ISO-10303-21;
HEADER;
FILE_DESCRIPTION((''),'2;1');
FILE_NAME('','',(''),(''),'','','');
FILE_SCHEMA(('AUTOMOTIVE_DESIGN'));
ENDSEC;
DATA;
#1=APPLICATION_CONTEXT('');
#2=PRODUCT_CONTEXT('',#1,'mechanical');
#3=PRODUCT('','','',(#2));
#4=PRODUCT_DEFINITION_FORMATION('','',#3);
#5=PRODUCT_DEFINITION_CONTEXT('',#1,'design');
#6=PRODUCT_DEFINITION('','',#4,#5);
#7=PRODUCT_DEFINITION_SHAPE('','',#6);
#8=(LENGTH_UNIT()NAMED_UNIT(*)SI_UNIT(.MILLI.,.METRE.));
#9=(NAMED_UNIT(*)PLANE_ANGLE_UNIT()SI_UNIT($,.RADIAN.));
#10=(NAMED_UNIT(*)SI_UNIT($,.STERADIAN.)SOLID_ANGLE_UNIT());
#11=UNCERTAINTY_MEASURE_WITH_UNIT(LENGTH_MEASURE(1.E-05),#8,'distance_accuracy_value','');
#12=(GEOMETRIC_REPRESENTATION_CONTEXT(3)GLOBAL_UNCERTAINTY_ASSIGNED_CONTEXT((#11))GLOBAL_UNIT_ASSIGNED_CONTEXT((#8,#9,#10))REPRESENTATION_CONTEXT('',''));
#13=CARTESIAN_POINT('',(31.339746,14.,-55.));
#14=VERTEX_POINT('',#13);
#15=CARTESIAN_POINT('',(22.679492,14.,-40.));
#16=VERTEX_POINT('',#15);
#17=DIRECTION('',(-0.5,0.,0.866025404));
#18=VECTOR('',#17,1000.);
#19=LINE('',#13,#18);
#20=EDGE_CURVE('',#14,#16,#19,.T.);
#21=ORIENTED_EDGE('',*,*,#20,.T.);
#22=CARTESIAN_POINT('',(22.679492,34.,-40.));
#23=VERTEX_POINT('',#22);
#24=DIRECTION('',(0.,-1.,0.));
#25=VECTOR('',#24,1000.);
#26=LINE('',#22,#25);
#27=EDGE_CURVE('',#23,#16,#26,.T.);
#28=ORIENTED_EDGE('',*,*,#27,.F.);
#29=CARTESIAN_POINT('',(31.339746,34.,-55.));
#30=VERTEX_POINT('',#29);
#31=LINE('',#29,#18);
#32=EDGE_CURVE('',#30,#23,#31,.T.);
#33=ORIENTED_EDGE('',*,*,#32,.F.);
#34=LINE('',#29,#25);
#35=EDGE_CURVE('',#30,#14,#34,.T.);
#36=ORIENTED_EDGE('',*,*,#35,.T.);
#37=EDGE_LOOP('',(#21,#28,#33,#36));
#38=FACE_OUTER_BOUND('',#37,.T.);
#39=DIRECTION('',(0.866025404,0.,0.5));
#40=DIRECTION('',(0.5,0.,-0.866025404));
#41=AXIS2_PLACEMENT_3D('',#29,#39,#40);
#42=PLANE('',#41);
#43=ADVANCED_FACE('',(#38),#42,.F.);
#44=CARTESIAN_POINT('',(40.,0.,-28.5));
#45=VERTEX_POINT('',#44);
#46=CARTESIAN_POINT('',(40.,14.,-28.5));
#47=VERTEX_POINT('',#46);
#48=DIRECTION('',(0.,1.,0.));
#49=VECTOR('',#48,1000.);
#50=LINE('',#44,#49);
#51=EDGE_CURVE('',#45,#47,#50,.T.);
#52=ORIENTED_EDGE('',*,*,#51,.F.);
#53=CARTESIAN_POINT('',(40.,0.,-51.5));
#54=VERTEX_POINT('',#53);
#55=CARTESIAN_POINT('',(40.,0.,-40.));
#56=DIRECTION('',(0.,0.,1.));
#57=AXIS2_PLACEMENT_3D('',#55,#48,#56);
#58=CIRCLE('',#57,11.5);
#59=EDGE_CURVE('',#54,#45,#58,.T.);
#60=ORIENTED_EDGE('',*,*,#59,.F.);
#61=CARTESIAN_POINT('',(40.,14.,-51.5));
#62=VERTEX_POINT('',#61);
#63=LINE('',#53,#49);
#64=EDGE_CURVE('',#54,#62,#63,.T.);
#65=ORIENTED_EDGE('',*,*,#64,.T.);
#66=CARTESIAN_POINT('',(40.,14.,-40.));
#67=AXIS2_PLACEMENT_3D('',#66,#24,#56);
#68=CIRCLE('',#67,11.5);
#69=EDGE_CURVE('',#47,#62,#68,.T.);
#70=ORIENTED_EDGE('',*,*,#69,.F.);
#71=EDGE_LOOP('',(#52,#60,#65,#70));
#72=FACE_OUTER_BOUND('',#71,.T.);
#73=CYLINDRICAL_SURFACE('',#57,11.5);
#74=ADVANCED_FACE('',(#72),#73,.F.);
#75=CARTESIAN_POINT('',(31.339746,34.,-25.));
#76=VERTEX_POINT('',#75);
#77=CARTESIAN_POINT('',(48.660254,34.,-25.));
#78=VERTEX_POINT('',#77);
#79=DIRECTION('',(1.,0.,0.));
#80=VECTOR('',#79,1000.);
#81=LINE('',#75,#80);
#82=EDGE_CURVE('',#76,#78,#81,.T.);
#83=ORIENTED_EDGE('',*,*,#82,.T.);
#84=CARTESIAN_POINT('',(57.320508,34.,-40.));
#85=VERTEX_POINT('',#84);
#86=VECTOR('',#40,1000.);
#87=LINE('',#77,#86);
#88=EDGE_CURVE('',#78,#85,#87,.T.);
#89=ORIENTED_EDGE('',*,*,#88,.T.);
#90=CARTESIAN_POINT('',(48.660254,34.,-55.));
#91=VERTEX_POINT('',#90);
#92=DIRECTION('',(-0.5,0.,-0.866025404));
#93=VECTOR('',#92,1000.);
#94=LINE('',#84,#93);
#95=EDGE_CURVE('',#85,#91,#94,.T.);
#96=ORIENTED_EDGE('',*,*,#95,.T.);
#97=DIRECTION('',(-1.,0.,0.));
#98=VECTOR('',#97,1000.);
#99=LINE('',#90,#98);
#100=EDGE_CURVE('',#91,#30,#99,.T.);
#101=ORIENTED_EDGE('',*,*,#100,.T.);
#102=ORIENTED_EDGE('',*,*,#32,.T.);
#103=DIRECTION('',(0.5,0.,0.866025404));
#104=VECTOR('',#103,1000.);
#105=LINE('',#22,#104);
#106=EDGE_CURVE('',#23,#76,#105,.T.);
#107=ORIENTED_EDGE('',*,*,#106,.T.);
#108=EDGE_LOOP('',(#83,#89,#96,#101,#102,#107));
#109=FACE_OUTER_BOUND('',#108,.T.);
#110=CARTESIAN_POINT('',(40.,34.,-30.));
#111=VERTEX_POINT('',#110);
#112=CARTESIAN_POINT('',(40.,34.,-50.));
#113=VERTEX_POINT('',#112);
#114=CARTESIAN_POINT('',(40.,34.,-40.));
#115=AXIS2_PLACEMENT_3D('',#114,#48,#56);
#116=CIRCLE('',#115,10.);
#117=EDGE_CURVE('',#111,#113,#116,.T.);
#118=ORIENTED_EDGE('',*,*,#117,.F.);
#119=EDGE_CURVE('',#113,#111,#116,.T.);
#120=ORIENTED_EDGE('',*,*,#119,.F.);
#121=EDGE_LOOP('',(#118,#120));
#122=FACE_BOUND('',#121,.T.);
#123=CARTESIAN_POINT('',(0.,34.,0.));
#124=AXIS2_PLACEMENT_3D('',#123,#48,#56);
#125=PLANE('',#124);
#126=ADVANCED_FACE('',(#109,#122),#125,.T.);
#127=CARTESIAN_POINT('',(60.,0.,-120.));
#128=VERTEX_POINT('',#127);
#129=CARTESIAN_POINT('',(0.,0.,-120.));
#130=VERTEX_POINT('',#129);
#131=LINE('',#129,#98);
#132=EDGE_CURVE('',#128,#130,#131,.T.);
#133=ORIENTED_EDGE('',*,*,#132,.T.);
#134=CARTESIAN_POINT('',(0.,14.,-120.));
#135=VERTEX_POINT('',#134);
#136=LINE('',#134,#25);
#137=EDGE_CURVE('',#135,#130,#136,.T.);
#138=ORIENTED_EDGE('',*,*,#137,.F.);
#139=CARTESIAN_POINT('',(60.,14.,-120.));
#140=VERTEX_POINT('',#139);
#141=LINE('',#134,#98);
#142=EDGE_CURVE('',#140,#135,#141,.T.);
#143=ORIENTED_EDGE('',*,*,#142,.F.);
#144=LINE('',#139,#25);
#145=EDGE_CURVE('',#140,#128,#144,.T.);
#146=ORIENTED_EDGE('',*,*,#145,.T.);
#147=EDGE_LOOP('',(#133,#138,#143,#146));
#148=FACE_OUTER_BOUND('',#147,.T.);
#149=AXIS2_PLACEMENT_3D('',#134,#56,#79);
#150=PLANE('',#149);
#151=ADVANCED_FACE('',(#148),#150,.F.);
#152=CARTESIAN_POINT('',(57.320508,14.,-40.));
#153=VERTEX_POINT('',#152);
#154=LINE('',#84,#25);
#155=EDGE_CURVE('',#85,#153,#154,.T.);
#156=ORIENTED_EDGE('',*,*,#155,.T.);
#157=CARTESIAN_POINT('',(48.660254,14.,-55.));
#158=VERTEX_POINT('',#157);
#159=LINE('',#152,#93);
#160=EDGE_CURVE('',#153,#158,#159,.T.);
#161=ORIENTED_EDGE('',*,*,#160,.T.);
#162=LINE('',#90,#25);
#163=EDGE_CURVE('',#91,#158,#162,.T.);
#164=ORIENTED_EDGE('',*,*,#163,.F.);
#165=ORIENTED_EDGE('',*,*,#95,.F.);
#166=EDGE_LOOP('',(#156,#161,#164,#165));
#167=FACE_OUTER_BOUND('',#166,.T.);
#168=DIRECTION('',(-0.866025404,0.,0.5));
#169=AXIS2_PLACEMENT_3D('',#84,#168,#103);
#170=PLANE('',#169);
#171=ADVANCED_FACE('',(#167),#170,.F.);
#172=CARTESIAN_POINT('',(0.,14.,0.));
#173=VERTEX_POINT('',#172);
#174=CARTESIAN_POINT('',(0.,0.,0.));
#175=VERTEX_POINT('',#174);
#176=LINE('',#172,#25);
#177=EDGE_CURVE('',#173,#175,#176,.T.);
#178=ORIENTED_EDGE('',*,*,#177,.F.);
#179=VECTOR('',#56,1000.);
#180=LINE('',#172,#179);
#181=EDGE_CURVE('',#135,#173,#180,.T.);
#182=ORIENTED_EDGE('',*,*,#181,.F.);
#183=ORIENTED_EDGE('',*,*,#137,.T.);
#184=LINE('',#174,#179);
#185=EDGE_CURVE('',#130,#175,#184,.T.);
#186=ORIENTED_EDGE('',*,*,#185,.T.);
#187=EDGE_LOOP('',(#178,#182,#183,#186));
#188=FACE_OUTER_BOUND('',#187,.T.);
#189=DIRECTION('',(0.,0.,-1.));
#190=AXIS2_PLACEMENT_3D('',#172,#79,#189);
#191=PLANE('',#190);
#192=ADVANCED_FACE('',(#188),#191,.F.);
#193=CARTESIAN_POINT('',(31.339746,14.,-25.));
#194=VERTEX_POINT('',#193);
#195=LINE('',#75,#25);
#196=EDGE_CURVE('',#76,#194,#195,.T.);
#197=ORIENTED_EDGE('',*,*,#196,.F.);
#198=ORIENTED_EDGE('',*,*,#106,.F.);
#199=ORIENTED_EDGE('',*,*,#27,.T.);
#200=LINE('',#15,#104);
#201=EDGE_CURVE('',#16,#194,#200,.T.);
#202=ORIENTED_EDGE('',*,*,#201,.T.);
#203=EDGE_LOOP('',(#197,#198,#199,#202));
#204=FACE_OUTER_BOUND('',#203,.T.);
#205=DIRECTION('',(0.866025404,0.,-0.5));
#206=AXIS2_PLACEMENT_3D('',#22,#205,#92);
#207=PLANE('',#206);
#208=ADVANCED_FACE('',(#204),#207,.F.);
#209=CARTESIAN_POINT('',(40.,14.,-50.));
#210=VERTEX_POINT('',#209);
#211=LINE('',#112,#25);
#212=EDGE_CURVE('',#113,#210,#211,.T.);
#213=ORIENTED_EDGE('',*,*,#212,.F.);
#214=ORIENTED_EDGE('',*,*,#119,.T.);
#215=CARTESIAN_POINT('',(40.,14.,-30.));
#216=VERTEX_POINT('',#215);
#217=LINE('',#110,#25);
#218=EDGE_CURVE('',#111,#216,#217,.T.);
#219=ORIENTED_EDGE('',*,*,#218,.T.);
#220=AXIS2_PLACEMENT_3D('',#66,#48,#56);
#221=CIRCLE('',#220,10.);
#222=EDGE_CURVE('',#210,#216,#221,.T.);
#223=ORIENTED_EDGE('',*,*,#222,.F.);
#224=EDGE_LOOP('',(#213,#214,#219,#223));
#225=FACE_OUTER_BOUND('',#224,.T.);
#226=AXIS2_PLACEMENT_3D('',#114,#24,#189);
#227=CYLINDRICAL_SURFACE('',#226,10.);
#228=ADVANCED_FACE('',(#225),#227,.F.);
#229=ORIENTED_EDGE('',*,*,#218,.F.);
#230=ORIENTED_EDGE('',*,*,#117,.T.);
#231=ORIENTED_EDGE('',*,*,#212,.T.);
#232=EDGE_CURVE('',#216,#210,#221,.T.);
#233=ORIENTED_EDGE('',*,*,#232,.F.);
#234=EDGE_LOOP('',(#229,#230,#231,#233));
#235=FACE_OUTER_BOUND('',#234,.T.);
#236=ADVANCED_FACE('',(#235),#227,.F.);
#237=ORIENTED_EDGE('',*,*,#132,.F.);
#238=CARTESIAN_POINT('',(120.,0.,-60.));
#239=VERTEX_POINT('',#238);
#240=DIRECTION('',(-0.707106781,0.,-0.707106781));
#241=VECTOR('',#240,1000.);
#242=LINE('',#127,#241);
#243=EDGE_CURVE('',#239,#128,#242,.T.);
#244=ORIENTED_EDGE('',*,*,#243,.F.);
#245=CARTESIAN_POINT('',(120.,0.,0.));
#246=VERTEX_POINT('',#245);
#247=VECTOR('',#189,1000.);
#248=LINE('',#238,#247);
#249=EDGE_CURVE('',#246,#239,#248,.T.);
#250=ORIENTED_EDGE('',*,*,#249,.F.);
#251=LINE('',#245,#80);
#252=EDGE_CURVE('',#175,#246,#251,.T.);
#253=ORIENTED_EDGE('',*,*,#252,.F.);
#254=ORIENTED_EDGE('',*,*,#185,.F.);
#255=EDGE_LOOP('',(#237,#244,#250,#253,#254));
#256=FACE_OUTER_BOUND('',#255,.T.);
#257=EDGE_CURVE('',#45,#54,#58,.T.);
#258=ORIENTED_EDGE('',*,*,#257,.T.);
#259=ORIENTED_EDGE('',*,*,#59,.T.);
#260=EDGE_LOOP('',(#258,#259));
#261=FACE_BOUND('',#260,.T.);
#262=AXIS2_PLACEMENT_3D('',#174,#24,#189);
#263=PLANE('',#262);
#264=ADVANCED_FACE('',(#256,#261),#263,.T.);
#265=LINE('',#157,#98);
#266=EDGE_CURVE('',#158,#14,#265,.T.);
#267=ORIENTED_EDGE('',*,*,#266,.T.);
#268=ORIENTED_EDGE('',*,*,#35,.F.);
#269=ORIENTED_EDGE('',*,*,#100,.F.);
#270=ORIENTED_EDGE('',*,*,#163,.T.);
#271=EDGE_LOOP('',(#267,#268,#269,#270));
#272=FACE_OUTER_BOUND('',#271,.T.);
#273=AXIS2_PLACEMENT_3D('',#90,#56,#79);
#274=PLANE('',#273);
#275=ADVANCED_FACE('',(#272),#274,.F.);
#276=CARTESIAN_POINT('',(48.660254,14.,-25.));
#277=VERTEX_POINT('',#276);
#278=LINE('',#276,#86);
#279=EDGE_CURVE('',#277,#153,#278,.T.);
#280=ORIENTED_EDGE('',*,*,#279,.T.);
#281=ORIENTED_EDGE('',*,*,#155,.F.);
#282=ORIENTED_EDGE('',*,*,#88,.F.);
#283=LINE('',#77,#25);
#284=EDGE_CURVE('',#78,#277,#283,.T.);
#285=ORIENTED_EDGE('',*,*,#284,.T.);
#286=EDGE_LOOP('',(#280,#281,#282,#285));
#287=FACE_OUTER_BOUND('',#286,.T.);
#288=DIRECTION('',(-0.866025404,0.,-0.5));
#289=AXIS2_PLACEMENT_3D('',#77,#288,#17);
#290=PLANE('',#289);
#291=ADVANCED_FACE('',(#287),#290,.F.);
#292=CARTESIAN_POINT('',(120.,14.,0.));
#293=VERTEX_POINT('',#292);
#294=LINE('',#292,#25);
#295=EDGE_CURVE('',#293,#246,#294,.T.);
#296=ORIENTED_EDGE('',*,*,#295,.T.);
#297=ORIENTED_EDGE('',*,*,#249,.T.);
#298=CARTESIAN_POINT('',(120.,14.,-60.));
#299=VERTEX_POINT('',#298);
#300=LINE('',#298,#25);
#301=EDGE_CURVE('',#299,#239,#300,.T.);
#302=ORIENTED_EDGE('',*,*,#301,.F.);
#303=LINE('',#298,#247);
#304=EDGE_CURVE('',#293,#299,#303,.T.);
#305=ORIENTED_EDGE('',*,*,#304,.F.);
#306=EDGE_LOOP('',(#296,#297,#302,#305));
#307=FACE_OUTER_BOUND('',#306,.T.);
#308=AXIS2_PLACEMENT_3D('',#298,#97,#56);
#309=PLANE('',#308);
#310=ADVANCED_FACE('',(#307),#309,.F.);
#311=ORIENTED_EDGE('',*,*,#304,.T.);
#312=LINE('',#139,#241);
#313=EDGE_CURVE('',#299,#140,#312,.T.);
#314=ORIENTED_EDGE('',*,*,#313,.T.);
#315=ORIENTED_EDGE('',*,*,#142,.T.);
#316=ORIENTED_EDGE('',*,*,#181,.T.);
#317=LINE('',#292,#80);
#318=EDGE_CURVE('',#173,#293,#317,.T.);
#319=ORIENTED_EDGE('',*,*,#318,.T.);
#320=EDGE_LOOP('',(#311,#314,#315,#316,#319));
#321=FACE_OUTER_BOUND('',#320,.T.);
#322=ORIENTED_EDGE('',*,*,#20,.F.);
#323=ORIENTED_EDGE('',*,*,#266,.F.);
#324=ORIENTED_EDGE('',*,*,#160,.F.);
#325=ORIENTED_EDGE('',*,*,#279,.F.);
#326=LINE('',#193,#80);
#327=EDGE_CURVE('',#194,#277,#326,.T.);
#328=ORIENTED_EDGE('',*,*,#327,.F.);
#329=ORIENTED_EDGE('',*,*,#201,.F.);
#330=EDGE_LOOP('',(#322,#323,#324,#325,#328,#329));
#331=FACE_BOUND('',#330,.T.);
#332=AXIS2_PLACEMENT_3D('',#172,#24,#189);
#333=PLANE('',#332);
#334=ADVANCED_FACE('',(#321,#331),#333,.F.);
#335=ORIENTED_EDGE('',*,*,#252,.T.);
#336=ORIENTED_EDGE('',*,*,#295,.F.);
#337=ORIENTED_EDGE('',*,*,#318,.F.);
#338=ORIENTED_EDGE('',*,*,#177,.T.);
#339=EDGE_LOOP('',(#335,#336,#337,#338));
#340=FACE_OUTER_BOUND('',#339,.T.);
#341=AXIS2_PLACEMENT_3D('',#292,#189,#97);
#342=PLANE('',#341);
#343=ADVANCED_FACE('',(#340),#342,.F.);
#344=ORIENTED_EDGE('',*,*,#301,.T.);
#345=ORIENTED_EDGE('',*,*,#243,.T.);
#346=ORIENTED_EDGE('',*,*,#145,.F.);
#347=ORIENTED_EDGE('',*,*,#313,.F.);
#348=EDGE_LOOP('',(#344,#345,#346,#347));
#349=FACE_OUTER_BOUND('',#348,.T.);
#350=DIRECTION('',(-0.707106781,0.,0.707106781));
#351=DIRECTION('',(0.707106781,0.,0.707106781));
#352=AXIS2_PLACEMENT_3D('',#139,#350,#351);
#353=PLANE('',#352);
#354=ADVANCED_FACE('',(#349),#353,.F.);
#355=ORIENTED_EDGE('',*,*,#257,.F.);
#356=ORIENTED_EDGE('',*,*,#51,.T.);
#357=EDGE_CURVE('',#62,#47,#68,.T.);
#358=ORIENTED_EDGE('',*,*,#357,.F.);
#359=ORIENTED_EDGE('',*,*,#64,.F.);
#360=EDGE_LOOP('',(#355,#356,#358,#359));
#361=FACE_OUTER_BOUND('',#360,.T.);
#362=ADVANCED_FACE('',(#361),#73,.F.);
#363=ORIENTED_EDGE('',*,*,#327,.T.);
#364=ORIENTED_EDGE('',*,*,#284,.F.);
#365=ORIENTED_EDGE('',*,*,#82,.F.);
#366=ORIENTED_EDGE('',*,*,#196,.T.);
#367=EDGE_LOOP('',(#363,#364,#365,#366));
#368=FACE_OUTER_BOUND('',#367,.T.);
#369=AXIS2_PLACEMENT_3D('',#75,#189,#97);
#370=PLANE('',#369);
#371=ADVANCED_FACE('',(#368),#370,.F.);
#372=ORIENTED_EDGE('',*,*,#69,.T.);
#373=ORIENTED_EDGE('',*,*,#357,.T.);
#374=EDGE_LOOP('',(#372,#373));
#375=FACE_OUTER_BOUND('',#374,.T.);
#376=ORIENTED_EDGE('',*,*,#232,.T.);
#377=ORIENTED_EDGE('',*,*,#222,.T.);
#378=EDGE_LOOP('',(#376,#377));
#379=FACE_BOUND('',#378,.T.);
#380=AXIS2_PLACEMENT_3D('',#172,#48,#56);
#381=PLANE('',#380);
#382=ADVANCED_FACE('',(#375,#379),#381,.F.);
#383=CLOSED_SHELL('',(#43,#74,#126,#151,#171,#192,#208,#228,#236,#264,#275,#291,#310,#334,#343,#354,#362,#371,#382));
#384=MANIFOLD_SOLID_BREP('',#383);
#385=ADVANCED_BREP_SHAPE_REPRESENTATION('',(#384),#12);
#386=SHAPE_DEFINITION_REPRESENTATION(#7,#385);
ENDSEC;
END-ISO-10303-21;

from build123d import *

# Parameters (mm, degrees)
BOSS_EXTRUDE1_DEPTH = 14
SKETCH3_R           = 11.5
CUT_EXTRUDE1_DEPTH  = 14
SKETCH4_R           = 10
BOSS_EXTRUDE2_DEPTH = 20


with BuildPart() as part:
    # Sketch2 → Boss-Extrude1 (new body)
    with BuildSketch(Plane(origin=(0, 0, 0), x_dir=(1, 0, 0), z_dir=(0, 1, 0))):
        Polygon((0, 0), (0, 120), (60, 120), (120, 60), (120, 0), align=None)
    extrude(amount=BOSS_EXTRUDE1_DEPTH)

    # Sketch3 → Cut-Extrude1 (cut)
    with BuildSketch(Plane(origin=(0, 14, 0), x_dir=(1, 0, 0), z_dir=(0, 1, 0))):
        with Locations(Location((40, 40, 0), (0, 0, 270))):
            Circle(SKETCH3_R)
    extrude(amount=-CUT_EXTRUDE1_DEPTH, mode=Mode.SUBTRACT)

    # Sketch4 → Boss-Extrude2 (add)
    with BuildSketch(Plane(origin=(0, 14, 0), x_dir=(1, 0, 0), z_dir=(0, 1, 0))):
        Polygon((57.320508076, 40), (48.660254038, 55), (31.339745962, 55), (22.679491924, 40), (31.339745962, 25), (48.660254038, 25), align=None)
        with Locations(Location((40, 40, 0), (0, 0, 270))):
            Circle(SKETCH4_R, mode=Mode.SUBTRACT)
    extrude(amount=BOSS_EXTRUDE2_DEPTH)


solid = part.part
